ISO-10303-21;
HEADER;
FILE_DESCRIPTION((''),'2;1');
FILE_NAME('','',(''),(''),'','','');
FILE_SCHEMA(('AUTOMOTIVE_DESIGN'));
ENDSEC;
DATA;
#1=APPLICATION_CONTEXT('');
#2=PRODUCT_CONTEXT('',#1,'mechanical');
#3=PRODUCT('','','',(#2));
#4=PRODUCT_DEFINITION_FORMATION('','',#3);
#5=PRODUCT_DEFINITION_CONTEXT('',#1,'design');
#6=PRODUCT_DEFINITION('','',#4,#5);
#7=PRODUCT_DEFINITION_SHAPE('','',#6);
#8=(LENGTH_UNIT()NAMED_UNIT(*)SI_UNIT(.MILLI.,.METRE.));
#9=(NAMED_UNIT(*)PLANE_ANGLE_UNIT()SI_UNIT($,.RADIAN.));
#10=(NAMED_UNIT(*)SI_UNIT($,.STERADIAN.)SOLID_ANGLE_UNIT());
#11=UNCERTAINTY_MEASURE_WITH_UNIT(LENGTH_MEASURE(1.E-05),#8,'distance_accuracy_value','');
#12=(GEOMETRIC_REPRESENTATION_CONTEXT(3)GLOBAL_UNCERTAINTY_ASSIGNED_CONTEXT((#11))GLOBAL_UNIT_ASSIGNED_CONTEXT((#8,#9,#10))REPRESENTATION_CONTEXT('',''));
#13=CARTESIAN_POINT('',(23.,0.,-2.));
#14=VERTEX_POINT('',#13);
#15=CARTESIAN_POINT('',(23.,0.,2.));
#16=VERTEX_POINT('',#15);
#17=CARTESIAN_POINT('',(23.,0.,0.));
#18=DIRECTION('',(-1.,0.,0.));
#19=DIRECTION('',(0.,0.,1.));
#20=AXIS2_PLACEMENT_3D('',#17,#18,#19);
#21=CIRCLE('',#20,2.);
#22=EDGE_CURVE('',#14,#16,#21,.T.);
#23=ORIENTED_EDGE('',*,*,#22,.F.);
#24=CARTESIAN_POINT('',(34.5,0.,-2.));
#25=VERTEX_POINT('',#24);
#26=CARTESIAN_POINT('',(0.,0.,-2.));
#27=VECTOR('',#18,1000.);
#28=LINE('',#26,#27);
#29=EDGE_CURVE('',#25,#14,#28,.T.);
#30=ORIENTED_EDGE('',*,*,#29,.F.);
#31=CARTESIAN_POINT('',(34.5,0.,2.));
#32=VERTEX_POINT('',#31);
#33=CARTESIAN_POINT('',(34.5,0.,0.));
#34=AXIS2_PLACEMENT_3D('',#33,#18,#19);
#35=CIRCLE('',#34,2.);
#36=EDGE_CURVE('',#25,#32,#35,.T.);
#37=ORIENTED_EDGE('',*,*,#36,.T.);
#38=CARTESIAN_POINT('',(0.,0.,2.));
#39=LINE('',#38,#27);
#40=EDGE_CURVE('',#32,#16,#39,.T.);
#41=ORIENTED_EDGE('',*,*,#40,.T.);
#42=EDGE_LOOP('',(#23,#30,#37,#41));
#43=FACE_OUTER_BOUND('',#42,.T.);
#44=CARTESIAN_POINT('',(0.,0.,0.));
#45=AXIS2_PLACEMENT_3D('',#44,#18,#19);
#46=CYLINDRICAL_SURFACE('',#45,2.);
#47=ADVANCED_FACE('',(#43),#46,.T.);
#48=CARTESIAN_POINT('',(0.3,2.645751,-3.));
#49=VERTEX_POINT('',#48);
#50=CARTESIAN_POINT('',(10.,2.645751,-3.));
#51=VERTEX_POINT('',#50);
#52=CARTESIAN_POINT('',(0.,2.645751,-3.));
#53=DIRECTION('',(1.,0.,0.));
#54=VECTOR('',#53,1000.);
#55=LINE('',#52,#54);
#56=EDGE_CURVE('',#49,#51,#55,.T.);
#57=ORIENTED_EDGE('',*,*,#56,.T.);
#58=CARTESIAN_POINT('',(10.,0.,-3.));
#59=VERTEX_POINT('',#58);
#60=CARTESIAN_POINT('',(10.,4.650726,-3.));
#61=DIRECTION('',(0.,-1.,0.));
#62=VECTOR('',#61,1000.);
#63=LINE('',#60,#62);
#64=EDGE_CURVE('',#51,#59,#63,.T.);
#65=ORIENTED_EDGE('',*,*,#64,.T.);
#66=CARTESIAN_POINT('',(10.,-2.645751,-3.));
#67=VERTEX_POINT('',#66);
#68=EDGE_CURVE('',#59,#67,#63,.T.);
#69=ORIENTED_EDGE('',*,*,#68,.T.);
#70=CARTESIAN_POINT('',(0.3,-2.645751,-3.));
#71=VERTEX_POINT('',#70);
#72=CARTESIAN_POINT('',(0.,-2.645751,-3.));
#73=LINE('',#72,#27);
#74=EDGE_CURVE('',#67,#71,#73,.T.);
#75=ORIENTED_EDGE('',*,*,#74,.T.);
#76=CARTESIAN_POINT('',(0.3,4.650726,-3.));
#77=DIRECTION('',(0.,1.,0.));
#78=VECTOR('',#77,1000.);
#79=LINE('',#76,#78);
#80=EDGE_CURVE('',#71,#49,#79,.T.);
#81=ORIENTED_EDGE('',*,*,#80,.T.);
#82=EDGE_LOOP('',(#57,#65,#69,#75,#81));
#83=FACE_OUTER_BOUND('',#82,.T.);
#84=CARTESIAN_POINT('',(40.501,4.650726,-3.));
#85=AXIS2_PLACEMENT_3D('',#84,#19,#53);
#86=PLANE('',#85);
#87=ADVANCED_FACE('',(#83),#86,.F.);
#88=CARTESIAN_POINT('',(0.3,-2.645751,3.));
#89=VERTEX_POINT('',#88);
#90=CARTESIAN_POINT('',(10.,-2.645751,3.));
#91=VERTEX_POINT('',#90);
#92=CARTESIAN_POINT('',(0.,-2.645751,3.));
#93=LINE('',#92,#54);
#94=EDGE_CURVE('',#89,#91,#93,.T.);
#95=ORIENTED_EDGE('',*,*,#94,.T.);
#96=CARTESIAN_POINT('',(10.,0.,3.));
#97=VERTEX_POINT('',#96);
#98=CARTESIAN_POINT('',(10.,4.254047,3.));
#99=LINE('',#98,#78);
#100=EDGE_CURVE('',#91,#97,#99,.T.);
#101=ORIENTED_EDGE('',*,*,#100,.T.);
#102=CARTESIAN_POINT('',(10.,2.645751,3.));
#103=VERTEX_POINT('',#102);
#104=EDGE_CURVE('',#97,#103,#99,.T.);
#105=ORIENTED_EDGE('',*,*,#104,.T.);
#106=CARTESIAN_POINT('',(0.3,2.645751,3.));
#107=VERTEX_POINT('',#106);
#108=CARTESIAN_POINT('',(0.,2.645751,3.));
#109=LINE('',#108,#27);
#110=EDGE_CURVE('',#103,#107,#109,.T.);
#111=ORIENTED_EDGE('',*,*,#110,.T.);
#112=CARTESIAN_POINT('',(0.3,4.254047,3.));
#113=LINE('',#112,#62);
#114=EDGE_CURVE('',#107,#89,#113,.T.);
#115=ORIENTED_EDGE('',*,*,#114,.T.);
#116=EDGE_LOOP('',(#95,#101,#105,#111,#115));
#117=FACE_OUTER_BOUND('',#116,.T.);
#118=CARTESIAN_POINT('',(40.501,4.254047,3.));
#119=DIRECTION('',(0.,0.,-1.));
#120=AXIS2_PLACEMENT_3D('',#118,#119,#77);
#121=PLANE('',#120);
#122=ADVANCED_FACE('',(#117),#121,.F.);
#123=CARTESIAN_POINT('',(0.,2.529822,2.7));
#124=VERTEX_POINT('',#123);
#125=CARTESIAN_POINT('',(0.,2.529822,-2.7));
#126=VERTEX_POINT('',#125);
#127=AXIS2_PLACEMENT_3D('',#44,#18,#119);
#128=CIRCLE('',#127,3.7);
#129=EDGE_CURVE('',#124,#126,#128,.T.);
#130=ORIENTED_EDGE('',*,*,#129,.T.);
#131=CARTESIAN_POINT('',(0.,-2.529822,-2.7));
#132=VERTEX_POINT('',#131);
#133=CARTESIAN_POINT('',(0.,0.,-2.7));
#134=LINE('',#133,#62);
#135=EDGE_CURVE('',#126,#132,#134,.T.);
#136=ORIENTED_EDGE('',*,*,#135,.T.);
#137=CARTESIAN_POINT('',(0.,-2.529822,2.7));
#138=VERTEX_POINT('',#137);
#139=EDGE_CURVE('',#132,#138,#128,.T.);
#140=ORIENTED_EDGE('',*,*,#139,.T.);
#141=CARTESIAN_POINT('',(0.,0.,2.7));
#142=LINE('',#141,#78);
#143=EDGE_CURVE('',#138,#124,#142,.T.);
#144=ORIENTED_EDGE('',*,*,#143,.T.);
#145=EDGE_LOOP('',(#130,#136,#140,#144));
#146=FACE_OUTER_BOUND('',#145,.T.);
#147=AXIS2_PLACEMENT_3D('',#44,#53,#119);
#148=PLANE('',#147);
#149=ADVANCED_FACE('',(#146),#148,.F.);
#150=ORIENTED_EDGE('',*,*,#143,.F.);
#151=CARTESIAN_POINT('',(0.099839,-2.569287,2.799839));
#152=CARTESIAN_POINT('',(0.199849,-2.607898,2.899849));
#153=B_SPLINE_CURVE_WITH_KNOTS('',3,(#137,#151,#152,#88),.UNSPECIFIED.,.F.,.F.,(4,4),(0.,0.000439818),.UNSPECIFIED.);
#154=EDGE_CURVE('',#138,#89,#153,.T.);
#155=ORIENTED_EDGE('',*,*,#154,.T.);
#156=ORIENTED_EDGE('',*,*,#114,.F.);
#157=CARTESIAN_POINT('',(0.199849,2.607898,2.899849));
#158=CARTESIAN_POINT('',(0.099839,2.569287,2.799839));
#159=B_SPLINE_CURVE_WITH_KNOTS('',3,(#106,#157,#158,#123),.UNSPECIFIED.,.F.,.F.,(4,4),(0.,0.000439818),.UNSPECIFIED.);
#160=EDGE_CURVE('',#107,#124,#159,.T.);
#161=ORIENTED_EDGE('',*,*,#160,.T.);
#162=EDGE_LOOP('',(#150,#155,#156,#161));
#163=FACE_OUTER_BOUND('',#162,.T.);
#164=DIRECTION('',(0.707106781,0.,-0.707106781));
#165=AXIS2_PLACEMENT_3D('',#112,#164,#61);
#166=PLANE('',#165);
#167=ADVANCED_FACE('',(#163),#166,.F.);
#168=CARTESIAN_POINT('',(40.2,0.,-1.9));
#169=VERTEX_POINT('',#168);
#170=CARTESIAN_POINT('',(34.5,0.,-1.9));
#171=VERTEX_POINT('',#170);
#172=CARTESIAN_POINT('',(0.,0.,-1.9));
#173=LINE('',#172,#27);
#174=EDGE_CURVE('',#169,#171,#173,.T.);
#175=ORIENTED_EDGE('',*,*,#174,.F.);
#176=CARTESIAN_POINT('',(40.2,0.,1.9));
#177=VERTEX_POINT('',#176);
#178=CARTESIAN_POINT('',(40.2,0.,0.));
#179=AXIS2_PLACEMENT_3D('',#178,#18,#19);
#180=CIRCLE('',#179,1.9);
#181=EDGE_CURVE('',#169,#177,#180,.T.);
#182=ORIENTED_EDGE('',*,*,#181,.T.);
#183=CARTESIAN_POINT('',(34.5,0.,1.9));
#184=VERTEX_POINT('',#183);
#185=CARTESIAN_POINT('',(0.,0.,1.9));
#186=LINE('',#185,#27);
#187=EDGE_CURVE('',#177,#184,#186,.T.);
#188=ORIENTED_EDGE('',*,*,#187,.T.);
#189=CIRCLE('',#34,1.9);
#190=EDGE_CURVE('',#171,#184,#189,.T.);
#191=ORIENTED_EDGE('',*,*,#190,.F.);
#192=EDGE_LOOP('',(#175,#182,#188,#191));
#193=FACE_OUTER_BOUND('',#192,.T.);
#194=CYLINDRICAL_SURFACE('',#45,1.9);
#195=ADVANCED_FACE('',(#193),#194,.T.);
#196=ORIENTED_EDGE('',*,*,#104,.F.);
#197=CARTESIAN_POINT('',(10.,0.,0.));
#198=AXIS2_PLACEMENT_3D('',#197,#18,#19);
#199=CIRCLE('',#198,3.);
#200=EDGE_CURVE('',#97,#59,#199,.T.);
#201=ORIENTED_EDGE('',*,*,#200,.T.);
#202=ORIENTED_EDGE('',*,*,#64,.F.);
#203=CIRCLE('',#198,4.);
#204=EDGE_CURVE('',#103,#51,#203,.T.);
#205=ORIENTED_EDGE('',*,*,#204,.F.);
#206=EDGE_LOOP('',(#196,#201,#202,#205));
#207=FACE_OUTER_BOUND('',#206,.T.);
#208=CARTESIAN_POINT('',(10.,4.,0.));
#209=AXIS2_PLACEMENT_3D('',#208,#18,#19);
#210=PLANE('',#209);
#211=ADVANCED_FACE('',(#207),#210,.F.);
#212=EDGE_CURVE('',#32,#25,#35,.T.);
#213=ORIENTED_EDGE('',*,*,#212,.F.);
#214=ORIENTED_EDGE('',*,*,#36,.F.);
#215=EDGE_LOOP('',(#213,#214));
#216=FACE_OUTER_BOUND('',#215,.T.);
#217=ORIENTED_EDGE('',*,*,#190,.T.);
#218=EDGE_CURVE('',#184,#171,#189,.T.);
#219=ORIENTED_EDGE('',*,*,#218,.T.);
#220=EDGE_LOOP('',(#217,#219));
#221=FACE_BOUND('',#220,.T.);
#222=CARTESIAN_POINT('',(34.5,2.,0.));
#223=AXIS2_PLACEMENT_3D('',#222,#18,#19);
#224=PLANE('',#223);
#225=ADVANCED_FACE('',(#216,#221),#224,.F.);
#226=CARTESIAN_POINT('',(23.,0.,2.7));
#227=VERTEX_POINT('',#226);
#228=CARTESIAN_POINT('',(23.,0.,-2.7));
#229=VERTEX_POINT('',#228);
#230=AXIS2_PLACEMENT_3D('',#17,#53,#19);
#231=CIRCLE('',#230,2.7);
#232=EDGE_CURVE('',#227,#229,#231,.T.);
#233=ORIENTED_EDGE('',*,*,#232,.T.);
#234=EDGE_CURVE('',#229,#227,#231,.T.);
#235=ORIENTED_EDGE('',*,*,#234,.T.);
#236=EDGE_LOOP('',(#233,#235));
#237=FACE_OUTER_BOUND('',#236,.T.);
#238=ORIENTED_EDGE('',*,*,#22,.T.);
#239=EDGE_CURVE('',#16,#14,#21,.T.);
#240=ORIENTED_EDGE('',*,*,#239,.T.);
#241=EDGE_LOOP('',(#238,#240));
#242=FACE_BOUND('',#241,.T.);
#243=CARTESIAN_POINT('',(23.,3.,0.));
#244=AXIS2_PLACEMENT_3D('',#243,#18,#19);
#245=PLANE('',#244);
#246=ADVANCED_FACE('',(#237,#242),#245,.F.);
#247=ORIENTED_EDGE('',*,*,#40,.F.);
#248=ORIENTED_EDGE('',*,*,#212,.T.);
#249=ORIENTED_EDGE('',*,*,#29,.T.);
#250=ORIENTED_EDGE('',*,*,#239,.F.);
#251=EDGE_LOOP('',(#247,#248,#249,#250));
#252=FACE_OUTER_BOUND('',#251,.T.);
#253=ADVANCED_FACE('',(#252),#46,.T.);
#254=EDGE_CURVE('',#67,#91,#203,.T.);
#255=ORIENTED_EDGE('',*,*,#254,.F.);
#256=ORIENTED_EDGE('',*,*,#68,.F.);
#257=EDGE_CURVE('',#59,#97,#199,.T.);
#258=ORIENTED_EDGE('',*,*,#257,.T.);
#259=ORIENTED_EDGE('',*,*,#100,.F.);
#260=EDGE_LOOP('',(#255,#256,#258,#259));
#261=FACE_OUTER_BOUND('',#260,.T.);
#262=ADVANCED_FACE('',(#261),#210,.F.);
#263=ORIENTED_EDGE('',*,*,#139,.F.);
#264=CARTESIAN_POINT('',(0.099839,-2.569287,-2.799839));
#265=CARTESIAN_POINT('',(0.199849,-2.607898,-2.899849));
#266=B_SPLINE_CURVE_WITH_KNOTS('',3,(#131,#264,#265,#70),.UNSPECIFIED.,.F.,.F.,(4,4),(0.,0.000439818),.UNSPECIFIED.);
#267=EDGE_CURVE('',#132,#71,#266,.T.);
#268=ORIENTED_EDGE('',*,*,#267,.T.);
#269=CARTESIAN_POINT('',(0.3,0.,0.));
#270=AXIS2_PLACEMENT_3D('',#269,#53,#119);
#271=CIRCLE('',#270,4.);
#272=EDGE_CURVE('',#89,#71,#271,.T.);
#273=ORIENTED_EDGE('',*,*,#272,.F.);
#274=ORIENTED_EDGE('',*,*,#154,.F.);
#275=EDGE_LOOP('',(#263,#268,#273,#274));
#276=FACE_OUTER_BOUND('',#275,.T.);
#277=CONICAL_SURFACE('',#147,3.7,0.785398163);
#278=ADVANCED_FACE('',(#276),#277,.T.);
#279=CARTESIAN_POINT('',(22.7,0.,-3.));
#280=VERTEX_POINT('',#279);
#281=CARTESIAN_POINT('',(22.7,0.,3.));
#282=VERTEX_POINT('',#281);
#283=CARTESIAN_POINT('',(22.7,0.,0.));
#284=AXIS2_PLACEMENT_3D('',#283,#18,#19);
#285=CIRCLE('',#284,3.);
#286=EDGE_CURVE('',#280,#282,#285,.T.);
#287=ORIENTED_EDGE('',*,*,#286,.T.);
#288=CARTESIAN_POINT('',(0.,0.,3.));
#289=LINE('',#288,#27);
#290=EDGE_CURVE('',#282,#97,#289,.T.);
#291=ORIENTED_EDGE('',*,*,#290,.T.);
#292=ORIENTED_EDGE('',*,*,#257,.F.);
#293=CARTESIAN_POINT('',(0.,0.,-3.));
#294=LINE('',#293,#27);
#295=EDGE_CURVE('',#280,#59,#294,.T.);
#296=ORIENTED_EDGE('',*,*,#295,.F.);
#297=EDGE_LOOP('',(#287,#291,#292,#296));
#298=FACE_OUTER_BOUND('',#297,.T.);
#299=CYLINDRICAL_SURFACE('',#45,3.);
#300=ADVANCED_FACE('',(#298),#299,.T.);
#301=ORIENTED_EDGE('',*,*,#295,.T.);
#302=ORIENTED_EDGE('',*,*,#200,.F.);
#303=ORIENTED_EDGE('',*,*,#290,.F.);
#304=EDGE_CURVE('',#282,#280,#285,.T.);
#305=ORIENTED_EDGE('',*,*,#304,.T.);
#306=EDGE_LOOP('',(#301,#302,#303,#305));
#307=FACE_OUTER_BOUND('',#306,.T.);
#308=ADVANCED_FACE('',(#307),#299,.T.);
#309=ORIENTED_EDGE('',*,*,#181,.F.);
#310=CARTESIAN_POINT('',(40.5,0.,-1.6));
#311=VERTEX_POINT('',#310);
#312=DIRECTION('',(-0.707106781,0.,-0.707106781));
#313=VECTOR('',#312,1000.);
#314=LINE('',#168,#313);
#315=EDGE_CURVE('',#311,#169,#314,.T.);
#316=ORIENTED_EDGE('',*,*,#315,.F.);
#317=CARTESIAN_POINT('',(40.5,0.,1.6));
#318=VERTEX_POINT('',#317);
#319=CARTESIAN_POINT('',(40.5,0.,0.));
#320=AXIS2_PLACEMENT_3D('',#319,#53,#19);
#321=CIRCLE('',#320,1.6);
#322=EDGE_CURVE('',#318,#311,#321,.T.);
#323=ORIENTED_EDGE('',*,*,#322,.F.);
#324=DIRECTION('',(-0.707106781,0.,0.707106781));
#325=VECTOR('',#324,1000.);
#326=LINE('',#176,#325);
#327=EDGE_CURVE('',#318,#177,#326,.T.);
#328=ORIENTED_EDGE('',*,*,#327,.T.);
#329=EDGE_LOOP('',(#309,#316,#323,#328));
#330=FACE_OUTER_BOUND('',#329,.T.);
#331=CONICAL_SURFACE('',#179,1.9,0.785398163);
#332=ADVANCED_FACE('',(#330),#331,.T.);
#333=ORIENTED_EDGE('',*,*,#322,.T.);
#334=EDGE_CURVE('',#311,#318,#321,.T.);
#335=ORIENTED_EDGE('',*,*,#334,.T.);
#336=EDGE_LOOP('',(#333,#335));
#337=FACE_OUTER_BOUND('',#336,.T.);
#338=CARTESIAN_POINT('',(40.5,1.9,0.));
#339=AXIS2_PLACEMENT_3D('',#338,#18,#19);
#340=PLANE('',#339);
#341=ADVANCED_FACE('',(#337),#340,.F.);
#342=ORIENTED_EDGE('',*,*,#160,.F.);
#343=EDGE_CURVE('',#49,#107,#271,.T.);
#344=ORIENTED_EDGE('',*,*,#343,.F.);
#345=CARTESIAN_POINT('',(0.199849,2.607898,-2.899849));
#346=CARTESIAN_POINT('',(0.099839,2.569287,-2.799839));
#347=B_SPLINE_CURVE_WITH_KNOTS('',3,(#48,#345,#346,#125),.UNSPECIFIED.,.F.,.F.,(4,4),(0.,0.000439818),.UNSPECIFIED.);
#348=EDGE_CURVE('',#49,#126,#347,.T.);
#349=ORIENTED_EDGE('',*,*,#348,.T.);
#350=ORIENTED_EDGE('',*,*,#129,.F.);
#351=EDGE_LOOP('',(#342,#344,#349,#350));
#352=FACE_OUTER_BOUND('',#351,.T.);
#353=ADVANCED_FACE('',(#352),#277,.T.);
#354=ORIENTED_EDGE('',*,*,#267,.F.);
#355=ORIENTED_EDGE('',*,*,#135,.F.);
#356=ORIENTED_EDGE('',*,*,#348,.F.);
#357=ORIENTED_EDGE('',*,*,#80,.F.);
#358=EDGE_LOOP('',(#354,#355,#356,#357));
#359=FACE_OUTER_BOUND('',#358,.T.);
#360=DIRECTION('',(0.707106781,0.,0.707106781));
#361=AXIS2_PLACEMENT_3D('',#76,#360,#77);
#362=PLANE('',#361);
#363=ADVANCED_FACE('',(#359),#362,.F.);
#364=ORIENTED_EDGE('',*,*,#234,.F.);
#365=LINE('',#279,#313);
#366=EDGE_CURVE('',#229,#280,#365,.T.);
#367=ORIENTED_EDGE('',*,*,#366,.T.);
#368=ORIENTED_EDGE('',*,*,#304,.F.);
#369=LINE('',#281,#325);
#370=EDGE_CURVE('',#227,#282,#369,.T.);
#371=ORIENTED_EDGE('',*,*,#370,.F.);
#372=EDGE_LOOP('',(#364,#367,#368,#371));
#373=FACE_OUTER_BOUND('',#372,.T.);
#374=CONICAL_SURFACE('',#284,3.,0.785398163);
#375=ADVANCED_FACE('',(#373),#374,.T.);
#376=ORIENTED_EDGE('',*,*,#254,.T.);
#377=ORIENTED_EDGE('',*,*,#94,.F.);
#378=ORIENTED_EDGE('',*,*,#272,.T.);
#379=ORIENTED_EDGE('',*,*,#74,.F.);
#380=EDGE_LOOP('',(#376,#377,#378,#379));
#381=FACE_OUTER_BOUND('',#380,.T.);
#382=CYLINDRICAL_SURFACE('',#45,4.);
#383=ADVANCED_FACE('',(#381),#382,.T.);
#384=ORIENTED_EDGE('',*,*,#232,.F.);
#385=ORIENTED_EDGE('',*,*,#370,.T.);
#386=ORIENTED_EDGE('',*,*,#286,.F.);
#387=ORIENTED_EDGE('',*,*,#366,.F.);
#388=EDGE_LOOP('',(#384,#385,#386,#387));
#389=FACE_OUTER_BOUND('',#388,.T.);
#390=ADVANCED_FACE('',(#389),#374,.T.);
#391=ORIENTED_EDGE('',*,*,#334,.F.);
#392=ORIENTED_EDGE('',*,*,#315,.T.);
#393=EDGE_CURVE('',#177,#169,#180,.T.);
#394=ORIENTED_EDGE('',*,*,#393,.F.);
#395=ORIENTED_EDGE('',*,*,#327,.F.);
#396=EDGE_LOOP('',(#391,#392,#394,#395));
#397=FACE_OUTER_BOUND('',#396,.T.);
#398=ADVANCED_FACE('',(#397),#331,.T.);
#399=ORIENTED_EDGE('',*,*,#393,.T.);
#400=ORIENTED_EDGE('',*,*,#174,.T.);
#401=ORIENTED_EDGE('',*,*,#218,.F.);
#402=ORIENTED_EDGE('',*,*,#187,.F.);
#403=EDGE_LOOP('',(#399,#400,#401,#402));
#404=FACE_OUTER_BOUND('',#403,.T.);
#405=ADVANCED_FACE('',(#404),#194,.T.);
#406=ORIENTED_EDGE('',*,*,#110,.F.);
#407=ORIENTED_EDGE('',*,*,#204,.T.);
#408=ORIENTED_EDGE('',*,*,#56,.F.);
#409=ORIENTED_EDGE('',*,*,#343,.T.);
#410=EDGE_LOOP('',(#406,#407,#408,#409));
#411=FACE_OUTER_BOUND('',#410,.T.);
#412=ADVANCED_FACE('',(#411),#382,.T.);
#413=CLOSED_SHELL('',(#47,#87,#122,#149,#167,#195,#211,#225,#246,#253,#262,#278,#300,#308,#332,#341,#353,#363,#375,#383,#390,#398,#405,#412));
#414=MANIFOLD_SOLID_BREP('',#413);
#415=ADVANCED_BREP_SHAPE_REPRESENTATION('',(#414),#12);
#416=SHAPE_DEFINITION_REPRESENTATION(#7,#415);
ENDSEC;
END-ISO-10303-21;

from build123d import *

# Parameters (mm, degrees)
CUT_EXTRUDE1_REACH = 42.893
SKETCH2_W          = 1
SKETCH2_H          = 9.301452206
SKETCH2_H_2        = 8.508093048
CHAMFER2_SIZE      = 0.3


with BuildPart() as part:
    # Sketch1 → Revolve1 (revolve)
    with BuildSketch(Plane.XY, mode=Mode.PRIVATE) as revolve1_sk:
        Polygon((0, 0), (40.5, 0), (40.5, 1.9), (34.5, 1.9), (34.5, 2), (23, 2), (23, 3), (10, 3), (10, 4), (0, 4), align=None)
    revolve(revolve1_sk.sketch.rotate(Axis((0, 0, 0), (1, 0, 0)), 90), axis=Axis((0, 0, 0), (1, 0, 0)))

    # Sketch2 → Cut-Extrude1 (cut, up to next)
    with BuildSketch(Plane.ZY, mode=Mode.PRIVATE) as cut_extrude1_sk1:
        with Locations((-3.5, 0)):
            Rectangle(SKETCH2_W, SKETCH2_H)
    cut_extrude1_tool1 = extrude(cut_extrude1_sk1.sketch, amount=-CUT_EXTRUDE1_REACH, mode=Mode.PRIVATE) & part.part
    # Sketch2 → Cut-Extrude1 (cut, up to next)
    with BuildSketch(Plane.ZY, mode=Mode.PRIVATE) as cut_extrude1_sk2:
        with Locations((3.5, 0)):
            Rectangle(SKETCH2_W, SKETCH2_H_2)
    cut_extrude1_tool2 = extrude(cut_extrude1_sk2.sketch, amount=-CUT_EXTRUDE1_REACH, mode=Mode.PRIVATE) & part.part
    add(cut_extrude1_tool1.solids().sort_by_distance((0, 0, -3.5))[0], mode=Mode.SUBTRACT)
    add(cut_extrude1_tool2.solids().sort_by_distance((0, 0, 3.5))[0], mode=Mode.SUBTRACT)

    # Chamfer2
    chamfer2_edges = [part.edges().sort_by_distance(p)[0] for p in [
        (23, 0, -3),
        (0, 4, 0),
        (0, -4, 0),
        (0, 0, -3),
        (0, 0, 3),
        (40.5, 0, -1.9),
    ]]
    chamfer(chamfer2_edges, length=CHAMFER2_SIZE)


solid = part.part
